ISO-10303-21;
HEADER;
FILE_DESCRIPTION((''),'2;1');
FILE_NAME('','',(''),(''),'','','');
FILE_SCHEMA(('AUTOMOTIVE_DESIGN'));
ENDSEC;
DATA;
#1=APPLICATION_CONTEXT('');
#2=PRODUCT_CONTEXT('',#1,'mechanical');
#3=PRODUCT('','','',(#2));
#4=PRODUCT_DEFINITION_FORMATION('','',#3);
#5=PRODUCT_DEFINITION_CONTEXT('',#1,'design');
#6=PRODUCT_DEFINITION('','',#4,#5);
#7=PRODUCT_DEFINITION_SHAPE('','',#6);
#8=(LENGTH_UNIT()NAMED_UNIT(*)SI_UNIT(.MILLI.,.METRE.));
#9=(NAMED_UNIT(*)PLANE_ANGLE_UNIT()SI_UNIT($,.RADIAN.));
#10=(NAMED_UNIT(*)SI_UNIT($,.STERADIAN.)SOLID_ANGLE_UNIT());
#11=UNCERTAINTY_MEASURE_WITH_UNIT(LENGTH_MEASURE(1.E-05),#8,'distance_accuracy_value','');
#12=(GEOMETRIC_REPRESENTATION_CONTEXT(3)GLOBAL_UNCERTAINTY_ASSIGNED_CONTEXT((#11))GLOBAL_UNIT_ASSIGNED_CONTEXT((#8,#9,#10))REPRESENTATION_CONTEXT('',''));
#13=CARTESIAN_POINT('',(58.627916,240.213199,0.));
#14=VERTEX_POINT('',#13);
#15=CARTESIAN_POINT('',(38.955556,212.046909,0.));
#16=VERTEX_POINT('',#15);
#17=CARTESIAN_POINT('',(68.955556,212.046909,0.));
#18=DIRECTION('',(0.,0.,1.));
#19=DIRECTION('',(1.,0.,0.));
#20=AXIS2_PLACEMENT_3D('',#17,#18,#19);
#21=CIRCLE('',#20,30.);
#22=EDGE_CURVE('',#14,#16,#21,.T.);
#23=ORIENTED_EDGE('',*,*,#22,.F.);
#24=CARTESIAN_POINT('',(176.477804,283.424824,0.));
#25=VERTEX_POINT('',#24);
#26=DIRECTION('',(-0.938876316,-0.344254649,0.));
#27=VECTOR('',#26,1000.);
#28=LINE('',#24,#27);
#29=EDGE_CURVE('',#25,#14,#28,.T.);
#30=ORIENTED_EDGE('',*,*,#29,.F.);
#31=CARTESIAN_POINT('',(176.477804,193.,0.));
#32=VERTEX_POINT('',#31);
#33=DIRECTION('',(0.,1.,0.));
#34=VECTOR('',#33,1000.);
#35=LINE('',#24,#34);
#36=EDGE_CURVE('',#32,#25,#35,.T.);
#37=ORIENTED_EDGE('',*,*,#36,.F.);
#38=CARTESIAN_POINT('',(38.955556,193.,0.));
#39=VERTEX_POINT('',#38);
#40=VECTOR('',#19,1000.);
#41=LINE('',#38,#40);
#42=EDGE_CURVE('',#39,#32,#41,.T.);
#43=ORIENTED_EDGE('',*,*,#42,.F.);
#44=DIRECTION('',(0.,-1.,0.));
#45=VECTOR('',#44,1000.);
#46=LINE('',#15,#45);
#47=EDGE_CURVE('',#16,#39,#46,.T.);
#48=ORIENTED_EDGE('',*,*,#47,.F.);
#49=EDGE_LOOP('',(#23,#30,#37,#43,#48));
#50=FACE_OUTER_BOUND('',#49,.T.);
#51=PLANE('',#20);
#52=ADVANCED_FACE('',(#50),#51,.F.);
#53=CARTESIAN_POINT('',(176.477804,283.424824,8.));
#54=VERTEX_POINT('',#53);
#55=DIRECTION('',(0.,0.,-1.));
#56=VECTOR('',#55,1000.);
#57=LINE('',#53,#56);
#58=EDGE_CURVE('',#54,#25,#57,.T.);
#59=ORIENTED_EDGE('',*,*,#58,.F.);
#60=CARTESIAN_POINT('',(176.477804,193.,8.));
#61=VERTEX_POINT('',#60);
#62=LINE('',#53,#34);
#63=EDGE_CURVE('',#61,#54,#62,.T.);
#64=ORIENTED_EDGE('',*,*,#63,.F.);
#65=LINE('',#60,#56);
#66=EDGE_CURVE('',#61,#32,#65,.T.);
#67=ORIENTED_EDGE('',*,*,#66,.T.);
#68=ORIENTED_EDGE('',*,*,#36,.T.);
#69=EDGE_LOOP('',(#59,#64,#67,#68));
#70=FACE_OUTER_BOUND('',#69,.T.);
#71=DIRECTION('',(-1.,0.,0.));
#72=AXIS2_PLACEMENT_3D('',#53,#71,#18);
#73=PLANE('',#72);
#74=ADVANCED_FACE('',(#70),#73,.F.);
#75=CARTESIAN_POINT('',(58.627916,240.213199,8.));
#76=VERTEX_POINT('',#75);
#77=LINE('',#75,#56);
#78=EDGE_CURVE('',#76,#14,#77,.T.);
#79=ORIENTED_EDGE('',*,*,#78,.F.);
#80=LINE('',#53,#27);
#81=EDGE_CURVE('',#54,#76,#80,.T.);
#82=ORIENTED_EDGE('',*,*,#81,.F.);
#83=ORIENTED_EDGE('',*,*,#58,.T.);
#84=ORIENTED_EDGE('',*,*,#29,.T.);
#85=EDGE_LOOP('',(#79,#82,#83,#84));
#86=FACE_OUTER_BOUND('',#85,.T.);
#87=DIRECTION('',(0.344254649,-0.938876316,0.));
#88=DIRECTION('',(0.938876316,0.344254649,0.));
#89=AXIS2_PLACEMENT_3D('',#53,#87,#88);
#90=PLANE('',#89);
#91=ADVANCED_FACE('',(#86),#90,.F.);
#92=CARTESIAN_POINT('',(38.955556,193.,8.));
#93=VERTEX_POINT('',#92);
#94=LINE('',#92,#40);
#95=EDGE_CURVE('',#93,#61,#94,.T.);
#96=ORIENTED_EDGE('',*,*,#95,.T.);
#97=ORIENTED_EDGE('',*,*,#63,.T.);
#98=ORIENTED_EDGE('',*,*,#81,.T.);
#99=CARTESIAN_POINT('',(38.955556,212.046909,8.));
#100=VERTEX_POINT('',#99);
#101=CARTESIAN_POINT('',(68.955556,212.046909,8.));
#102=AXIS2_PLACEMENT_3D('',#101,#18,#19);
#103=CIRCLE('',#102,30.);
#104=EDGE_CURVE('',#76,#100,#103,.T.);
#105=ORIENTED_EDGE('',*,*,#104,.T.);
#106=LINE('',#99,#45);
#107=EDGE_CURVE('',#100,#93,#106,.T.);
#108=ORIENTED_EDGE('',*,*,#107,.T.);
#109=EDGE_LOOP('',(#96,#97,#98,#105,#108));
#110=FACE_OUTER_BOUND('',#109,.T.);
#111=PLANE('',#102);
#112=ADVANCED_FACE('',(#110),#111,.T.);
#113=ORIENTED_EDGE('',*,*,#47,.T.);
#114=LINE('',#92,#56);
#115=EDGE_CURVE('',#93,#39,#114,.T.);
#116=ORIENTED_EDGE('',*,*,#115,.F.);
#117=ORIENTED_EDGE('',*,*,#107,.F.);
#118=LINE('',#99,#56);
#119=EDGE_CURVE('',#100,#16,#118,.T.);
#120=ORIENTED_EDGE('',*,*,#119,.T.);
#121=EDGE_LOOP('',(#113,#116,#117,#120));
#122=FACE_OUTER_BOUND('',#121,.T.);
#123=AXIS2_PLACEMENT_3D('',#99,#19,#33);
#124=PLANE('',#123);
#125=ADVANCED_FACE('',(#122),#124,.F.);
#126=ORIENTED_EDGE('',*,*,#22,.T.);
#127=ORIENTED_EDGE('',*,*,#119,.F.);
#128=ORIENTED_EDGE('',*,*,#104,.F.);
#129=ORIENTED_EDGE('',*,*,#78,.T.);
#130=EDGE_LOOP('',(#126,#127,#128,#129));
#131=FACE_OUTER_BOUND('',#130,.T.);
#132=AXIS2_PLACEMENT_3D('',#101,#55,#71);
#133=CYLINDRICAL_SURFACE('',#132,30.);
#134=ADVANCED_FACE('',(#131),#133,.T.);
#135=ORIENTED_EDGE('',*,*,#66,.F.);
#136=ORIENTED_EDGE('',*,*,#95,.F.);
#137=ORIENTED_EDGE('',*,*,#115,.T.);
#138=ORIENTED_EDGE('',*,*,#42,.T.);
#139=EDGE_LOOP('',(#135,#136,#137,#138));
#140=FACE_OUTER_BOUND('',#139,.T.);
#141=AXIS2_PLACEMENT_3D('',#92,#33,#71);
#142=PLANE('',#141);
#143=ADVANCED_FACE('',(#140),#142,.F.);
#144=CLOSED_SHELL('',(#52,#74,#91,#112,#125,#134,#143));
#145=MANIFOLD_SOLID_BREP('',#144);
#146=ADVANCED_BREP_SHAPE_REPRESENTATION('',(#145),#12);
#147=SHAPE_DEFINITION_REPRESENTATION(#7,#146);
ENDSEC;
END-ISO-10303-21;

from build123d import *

# Parameters (mm, degrees)
EXTRUDE_1_DEPTH = 8


with BuildPart() as part:
    # 草图1 → 凸台-拉伸1 (new body)
    with BuildSketch(Plane(origin=(0, 0, 0), x_dir=(-1, 0, 0), z_dir=(0, 0, 1))):
        with BuildLine():
            Line((-176.477803528, -283.424824257), (-58.627916081, -240.213198859))
            ThreePointArc((-58.627916081, -240.213198859), (-44.360544026, -229.22495956), (-38.955555556, -212.046909383))
            Line((-38.955555556, -212.046909383), (-38.955555556, -193))
            Line((-38.955555556, -193), (-176.477803528, -193))
            Line((-176.477803528, -193), (-176.477803528, -283.424824257))
        make_face()
    extrude(amount=EXTRUDE_1_DEPTH)


solid = part.part
